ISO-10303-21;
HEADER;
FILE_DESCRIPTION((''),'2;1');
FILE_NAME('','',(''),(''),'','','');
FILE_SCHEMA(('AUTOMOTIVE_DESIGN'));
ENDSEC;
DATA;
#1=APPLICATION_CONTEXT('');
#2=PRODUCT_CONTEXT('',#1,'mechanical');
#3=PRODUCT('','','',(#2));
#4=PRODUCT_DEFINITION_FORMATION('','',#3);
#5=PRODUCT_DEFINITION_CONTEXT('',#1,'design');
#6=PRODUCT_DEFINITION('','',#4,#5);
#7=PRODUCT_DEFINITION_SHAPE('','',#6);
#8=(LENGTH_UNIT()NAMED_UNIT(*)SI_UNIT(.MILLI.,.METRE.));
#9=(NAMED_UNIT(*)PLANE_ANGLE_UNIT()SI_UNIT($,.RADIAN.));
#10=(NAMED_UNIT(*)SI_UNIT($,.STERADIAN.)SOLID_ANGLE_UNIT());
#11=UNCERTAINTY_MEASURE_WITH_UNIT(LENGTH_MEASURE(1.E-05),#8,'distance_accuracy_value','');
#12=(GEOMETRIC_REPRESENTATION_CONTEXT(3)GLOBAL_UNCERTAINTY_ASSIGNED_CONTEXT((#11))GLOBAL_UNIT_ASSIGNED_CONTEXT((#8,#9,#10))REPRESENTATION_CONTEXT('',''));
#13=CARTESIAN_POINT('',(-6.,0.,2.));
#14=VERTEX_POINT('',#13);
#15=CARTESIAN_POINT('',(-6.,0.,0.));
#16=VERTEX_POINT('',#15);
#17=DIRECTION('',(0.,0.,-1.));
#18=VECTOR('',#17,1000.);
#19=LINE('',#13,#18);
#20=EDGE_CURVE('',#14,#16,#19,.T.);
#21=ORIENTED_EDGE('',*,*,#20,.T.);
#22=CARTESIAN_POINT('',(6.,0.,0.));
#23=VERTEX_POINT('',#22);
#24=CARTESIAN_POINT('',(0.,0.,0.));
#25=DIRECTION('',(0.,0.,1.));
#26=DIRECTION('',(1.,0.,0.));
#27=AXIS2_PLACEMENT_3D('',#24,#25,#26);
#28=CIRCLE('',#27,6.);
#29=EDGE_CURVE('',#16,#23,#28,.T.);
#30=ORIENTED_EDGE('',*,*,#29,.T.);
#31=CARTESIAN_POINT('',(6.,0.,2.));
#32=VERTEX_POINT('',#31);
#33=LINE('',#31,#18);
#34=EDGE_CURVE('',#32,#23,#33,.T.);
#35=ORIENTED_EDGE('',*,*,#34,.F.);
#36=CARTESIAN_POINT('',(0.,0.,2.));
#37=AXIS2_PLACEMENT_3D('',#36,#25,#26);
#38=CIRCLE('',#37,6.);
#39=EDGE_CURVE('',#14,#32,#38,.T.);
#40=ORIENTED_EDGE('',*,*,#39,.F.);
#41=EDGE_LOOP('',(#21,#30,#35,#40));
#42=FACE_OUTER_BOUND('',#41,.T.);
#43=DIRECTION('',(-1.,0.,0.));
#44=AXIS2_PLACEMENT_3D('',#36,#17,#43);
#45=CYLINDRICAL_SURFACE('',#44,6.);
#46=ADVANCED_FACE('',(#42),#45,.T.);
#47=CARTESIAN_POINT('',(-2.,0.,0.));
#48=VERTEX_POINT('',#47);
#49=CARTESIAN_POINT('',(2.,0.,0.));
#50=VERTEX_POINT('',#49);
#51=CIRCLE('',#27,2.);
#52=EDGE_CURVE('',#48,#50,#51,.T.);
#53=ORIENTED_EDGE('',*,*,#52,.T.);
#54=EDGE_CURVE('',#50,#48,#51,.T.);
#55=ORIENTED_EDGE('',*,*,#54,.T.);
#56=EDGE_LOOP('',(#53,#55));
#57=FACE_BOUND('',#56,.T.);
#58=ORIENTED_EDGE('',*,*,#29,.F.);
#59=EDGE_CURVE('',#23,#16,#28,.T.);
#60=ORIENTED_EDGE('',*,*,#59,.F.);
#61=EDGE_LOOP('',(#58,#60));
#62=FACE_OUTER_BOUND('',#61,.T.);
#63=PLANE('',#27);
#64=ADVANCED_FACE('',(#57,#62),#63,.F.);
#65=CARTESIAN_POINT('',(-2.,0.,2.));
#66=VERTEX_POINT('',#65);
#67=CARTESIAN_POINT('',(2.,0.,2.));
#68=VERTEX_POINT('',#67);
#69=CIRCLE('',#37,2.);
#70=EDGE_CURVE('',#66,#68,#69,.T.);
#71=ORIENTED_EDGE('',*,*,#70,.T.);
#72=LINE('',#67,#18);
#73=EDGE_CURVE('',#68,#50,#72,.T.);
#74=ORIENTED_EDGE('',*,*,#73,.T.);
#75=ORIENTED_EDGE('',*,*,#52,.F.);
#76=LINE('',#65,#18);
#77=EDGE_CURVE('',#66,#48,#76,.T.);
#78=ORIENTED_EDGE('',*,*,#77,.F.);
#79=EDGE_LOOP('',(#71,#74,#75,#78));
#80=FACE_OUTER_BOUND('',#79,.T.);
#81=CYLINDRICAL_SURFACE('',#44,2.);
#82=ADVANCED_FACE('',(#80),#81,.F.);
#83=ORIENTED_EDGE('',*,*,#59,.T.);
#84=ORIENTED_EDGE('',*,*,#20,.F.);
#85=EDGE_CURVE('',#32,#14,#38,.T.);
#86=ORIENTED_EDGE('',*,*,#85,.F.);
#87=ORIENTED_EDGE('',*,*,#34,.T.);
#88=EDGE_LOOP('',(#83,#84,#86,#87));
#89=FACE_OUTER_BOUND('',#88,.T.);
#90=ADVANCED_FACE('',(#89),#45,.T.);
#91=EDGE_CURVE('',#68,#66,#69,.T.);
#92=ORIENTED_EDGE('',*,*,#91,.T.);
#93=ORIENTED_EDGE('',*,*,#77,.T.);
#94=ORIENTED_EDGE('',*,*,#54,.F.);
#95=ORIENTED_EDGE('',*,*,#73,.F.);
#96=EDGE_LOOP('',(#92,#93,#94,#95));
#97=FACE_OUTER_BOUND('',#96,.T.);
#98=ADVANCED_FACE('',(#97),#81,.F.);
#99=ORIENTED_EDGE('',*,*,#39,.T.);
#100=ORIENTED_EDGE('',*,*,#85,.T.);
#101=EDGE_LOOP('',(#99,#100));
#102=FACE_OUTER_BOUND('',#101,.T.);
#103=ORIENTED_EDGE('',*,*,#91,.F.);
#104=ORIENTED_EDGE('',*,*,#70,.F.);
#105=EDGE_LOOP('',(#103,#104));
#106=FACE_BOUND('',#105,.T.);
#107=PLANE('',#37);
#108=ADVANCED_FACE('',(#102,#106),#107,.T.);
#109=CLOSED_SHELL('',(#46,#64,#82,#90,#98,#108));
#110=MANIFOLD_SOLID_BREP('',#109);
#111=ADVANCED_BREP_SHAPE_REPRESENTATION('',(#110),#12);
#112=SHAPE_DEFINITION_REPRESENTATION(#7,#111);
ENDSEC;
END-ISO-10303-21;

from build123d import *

# Parameters (mm, degrees)
SKETCH_1_R      = 6
SKETCH_1_R_2    = 2
EXTRUDE_1_DEPTH = 2


with BuildPart() as part:
    # 草图1 → 凸台-拉伸1 (new body)
    with BuildSketch(Plane.XY):
        Circle(SKETCH_1_R)
        Circle(SKETCH_1_R_2, mode=Mode.SUBTRACT)
    extrude(amount=EXTRUDE_1_DEPTH)


solid = part.part
